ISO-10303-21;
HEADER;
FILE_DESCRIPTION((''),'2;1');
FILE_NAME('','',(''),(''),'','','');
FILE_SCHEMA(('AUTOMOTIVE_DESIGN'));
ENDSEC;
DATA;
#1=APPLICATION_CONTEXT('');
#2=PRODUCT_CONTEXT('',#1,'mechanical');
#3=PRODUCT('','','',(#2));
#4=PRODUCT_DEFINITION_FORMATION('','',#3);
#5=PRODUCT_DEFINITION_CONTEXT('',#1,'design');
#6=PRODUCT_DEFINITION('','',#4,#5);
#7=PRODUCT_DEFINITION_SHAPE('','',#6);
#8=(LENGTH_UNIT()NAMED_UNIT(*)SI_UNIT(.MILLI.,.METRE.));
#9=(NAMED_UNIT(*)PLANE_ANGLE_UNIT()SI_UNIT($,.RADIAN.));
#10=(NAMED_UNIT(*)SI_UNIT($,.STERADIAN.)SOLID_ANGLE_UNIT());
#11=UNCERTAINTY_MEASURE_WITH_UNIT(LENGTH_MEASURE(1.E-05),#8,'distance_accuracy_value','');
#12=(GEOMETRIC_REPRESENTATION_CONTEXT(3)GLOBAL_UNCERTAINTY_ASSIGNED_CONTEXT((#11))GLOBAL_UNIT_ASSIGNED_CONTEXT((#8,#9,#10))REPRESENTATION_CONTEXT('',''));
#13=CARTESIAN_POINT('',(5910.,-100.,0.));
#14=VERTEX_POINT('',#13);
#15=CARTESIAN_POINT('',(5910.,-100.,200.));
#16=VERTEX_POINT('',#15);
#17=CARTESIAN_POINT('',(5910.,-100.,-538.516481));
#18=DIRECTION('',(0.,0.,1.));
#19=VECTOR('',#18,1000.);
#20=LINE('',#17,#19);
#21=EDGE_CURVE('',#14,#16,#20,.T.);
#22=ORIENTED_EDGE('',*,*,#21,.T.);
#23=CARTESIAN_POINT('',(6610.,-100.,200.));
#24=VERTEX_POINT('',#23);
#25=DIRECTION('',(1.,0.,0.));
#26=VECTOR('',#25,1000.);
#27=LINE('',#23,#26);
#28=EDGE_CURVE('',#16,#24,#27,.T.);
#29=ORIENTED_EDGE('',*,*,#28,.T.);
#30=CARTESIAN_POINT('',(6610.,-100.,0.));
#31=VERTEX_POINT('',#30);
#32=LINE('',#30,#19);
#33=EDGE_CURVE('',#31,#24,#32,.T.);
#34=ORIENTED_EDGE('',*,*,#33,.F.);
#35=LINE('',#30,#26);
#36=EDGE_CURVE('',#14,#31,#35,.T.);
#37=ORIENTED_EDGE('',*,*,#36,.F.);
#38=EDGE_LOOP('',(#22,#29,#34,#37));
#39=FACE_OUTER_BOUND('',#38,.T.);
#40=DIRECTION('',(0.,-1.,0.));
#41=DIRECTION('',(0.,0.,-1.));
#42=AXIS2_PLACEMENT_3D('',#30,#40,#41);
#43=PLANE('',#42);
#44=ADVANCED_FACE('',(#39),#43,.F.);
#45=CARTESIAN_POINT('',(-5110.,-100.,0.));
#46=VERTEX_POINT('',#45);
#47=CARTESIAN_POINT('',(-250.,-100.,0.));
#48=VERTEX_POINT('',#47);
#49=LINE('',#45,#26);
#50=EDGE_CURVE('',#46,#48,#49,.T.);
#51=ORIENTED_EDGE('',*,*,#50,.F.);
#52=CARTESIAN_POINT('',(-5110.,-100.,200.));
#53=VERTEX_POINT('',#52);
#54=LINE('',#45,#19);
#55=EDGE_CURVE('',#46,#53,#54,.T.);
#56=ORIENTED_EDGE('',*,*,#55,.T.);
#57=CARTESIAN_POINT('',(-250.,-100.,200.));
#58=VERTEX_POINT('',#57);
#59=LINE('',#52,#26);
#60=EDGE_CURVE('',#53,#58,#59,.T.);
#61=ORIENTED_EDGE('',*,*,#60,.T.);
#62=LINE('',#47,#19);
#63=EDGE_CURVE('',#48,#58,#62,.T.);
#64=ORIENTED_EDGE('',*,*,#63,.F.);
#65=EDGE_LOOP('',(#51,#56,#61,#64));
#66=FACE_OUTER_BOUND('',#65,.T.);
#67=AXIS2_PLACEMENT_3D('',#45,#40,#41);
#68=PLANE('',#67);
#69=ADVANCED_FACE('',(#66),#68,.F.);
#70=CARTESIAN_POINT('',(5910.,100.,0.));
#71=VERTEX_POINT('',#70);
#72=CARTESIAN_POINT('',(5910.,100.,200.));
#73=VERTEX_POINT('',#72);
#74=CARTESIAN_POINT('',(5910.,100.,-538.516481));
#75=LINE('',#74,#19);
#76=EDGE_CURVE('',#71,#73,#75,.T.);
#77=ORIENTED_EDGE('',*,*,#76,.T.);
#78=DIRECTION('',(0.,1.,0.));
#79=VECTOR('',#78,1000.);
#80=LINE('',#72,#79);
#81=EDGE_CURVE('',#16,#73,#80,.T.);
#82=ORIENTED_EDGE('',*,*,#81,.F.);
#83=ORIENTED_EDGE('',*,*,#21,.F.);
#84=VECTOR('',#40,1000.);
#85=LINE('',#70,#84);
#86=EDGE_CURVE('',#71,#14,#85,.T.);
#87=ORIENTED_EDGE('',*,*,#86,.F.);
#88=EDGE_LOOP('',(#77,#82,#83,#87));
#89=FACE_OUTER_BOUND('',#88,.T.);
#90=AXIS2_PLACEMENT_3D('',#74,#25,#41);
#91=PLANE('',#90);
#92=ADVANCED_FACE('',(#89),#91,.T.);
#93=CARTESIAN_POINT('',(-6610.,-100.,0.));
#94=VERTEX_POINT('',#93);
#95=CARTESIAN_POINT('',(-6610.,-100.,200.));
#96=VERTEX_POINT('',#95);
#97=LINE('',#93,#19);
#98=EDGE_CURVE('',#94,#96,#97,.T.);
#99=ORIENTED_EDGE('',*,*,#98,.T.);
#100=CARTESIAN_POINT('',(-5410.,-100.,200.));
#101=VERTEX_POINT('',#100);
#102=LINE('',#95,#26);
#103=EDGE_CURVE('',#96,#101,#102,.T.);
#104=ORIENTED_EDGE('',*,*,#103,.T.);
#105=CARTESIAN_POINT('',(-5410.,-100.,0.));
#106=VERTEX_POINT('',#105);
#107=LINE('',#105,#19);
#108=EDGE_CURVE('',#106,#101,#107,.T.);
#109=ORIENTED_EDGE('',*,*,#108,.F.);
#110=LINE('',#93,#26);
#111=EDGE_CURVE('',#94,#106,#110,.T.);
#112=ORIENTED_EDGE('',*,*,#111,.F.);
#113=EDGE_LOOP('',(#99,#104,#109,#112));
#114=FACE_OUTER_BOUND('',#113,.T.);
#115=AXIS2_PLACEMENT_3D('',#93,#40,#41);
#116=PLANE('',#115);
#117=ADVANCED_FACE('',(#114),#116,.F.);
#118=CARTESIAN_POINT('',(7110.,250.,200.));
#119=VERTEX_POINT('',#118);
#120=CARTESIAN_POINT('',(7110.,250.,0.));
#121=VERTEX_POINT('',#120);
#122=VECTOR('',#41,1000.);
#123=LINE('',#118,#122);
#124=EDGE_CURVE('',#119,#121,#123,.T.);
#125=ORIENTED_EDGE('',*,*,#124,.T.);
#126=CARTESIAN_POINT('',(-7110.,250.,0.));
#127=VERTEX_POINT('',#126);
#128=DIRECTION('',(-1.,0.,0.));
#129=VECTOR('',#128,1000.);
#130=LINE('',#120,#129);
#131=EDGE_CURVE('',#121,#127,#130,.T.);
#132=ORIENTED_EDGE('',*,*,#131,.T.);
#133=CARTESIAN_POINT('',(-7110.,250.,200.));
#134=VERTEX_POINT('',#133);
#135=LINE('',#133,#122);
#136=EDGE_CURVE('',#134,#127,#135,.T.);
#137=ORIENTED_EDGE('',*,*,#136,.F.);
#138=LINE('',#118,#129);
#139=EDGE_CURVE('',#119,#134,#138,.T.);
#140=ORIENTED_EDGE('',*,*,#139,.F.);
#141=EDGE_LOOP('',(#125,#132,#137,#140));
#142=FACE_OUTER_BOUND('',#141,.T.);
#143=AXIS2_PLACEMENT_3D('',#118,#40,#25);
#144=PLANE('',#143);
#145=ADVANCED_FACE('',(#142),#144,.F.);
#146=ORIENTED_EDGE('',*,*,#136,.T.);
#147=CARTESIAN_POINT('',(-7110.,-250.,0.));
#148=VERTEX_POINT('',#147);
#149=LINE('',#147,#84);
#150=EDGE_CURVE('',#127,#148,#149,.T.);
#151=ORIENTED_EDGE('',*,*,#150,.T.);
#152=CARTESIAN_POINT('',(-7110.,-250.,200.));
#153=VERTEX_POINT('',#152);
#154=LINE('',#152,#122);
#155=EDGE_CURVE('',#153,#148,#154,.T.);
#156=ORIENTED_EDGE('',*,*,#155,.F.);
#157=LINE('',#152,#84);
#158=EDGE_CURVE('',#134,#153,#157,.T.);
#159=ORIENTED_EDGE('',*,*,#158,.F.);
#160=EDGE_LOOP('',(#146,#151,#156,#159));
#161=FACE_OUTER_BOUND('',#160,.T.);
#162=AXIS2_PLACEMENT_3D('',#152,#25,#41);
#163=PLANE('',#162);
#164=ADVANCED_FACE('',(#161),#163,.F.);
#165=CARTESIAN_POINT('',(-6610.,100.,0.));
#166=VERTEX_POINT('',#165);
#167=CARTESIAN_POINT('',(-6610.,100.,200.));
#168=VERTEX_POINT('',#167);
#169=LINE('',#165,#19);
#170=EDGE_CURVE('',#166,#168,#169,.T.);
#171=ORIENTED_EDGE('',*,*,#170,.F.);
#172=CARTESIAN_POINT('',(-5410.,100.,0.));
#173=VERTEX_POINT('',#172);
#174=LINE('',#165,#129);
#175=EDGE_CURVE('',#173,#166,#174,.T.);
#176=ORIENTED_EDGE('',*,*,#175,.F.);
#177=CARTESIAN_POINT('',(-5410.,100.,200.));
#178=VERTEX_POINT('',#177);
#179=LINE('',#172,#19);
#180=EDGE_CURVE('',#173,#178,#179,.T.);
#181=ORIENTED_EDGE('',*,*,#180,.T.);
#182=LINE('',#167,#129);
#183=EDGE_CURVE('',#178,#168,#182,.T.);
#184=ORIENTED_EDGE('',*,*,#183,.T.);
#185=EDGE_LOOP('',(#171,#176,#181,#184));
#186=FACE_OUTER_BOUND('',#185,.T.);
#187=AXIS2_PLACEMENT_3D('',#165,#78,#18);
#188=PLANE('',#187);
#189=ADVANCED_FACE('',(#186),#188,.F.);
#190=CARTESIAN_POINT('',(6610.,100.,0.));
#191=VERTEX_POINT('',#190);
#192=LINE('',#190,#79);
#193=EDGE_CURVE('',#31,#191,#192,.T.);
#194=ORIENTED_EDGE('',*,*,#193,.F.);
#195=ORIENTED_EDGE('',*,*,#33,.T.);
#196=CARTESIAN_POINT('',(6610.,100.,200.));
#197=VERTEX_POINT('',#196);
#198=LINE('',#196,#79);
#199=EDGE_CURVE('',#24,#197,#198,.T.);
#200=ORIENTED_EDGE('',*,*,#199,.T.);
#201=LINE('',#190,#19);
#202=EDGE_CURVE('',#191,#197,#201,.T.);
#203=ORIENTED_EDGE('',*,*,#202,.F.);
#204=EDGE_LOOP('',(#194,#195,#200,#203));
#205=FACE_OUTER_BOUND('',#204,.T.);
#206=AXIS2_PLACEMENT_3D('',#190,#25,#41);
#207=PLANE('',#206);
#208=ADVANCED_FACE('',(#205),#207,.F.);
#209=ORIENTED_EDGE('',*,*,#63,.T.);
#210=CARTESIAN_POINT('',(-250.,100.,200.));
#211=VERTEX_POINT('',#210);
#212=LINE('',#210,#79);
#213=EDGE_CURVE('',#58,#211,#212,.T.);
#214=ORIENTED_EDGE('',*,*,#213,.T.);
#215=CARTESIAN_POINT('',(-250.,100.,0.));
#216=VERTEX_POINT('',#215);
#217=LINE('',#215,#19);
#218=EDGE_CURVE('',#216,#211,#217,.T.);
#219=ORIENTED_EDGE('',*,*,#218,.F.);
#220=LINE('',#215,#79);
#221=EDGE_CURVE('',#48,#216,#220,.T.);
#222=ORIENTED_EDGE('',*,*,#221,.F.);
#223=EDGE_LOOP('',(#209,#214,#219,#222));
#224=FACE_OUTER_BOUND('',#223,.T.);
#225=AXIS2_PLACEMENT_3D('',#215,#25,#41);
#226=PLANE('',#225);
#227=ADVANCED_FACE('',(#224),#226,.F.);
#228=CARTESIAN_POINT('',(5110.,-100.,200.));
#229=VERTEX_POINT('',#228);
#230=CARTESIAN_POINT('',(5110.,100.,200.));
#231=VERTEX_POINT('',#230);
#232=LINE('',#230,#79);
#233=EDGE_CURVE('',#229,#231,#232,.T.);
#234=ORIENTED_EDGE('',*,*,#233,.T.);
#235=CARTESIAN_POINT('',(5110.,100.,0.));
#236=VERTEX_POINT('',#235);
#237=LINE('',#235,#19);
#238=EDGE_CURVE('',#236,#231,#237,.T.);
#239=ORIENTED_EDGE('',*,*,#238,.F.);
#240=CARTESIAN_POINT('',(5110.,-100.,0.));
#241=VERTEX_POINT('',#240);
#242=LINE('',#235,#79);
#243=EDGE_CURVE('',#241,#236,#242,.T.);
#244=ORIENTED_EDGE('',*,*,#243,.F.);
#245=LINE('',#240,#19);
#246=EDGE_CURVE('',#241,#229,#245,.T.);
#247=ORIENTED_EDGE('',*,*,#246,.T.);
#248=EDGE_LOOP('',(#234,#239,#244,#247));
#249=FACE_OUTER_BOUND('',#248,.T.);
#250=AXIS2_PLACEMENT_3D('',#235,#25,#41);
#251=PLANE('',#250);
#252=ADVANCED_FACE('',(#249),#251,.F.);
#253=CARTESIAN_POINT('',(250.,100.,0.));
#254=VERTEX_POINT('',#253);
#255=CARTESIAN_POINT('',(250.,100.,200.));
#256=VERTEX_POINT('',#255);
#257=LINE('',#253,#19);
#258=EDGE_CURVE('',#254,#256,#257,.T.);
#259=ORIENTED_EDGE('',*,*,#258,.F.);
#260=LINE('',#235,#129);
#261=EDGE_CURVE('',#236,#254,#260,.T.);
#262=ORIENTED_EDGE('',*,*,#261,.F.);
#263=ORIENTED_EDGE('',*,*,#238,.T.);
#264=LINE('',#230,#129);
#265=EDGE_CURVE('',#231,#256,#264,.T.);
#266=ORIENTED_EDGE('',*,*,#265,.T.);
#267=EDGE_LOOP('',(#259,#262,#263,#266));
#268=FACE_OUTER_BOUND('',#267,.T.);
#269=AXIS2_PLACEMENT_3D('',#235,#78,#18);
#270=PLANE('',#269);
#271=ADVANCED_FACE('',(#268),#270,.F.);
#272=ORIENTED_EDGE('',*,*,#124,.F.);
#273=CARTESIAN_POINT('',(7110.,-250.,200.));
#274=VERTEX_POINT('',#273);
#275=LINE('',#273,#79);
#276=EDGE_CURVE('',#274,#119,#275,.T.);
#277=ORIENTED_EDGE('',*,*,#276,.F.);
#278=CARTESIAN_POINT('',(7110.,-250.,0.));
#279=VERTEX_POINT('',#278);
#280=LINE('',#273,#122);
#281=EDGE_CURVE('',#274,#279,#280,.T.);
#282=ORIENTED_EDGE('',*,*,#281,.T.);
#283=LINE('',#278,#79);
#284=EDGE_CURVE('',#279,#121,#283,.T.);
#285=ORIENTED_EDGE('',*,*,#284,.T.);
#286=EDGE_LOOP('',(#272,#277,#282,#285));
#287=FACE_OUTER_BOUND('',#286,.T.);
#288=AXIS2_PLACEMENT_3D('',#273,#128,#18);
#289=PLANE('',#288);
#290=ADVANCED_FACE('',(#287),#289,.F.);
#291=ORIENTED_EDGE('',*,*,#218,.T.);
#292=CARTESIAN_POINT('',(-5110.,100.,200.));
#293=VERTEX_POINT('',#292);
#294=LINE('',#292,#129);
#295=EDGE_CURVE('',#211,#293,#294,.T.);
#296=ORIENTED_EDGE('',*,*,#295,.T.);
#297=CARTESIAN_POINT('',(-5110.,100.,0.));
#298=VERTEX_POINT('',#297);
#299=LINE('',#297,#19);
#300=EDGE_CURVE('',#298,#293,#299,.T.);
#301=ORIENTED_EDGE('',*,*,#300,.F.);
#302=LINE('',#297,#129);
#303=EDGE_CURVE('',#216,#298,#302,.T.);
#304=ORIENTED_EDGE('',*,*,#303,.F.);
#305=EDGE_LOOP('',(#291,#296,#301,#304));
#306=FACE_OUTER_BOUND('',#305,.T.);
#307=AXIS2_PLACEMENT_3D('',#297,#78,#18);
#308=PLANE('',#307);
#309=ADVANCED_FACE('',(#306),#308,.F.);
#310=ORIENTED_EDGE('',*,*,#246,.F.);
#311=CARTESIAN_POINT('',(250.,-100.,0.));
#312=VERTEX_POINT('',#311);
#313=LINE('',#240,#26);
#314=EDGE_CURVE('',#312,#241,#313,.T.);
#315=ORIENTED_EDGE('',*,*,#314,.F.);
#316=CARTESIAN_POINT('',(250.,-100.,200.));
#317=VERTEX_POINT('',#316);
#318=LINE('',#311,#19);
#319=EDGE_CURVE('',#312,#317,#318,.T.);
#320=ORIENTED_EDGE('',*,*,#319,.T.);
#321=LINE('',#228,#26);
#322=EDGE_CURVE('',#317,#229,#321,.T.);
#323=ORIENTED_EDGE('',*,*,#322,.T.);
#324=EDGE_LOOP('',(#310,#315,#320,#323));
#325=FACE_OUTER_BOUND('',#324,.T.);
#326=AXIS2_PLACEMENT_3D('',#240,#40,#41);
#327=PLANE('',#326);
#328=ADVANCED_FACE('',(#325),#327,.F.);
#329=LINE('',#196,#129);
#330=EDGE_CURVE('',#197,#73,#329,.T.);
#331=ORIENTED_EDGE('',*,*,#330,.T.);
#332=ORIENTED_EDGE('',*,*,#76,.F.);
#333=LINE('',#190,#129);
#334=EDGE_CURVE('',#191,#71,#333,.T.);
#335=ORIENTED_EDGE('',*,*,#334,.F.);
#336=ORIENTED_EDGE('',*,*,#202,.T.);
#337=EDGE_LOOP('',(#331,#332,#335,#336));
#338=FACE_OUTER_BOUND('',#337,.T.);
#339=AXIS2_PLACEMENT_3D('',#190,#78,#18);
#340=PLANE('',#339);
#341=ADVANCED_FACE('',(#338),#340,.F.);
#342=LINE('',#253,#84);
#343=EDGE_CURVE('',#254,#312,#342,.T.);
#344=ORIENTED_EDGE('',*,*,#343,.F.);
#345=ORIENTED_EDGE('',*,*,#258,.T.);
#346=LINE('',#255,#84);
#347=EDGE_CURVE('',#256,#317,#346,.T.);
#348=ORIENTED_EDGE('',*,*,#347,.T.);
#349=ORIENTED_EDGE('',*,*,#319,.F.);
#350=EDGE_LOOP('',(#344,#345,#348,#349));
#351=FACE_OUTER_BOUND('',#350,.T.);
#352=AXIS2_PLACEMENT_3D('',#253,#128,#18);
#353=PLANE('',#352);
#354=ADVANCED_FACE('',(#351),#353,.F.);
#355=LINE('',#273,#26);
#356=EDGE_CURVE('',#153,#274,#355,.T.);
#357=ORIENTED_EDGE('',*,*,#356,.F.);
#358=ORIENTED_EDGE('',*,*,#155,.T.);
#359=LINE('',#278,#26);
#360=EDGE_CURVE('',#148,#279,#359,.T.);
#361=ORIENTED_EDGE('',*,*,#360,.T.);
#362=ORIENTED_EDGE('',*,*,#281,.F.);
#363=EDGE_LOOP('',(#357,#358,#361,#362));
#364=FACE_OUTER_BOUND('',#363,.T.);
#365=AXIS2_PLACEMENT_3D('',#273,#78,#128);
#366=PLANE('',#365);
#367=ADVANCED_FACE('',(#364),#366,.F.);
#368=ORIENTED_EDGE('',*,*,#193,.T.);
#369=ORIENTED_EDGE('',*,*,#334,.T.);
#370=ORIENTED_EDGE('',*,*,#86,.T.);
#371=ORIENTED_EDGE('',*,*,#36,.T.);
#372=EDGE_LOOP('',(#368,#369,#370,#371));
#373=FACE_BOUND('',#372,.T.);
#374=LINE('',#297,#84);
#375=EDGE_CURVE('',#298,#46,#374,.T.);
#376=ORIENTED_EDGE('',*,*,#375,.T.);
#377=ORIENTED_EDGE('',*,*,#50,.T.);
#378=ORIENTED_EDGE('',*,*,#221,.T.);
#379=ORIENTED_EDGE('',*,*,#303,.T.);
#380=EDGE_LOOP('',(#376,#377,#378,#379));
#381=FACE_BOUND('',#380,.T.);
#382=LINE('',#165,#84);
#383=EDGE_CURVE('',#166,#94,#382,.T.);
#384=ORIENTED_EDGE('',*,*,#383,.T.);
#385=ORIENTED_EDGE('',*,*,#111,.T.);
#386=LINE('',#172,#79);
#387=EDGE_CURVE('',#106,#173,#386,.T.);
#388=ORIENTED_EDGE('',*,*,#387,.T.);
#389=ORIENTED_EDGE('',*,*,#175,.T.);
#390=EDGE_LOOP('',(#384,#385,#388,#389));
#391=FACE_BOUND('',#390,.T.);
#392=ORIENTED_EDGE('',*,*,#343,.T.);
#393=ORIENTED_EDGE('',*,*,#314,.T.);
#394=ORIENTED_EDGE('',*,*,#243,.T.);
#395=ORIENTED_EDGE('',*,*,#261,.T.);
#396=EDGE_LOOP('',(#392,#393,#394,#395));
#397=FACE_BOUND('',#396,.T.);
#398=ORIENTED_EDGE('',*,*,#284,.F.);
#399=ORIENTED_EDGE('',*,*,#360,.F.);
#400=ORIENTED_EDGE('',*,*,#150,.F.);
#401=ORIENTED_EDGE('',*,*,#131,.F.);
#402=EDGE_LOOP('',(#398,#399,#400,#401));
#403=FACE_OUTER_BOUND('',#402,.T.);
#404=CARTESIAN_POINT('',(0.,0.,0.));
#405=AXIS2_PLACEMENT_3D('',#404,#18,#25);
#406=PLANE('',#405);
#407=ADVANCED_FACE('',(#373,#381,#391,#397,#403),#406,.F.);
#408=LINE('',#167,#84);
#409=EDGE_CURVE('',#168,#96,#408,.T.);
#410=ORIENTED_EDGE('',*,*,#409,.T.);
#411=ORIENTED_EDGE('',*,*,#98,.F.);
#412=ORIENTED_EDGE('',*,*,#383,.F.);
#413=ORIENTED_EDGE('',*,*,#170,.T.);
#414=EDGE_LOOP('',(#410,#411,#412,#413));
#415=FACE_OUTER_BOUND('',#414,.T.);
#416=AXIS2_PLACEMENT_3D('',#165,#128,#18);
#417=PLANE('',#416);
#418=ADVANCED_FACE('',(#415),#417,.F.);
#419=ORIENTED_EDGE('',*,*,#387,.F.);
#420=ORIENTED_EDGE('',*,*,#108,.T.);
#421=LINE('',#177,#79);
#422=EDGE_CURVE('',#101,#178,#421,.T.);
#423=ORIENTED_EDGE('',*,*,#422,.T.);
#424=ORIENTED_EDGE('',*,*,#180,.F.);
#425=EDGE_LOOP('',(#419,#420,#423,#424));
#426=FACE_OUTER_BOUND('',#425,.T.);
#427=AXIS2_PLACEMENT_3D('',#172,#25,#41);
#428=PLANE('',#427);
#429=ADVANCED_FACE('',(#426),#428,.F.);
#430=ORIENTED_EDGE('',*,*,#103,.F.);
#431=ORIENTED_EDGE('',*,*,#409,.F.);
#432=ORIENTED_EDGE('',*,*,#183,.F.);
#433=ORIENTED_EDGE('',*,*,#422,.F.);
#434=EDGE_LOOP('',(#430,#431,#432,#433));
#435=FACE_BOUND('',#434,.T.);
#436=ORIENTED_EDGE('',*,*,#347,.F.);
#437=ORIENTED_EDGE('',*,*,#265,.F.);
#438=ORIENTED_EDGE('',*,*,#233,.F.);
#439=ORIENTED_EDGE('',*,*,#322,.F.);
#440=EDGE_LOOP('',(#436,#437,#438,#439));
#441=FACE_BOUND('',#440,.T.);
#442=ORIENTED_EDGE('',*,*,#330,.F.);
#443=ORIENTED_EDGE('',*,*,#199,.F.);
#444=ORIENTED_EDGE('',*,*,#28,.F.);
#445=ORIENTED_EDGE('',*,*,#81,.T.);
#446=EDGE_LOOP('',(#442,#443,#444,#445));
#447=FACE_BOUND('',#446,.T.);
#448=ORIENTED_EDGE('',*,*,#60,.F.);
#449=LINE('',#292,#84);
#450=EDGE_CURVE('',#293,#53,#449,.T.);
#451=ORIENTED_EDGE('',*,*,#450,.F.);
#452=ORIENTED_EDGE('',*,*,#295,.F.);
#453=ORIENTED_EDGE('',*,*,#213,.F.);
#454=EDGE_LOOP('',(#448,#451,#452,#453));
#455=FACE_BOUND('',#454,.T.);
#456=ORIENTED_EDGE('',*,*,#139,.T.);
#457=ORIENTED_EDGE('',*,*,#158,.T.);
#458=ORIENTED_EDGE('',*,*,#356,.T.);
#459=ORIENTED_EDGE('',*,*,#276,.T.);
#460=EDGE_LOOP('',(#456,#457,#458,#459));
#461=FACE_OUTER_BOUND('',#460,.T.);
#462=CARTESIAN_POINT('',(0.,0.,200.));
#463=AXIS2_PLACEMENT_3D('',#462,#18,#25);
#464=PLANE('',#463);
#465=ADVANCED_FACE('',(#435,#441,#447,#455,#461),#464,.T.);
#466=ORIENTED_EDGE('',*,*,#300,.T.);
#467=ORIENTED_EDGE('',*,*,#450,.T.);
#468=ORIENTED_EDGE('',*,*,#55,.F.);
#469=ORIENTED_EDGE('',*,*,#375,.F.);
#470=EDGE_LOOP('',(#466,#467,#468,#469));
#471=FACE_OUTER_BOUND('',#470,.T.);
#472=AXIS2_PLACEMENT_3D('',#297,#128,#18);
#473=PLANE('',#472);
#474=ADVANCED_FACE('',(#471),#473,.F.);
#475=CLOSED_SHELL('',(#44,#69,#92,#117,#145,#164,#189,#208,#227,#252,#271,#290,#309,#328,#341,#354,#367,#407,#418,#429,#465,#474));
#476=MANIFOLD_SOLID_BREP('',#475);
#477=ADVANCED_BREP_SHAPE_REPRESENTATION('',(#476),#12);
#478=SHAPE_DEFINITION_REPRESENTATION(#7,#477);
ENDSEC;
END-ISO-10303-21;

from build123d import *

# Parameters (mm, degrees)
SKETCH1_W           = 14220
SKETCH1_H           = 500
BOSS_EXTRUDE1_DEPTH = 200
SKETCH2_W           = 1200
SKETCH2_H           = 200
SKETCH2_W_2         = 4860
CUT_EXTRUDE1_DEPTH  = 7118.204507389
SKETCH4_W           = 500
SKETCH4_H           = 200
BOSS_EXTRUDE2_DEPTH = 200


with BuildPart() as part:
    # Sketch1 → Boss-Extrude1 (new body)
    with BuildSketch(Plane.XY):
        Rectangle(SKETCH1_W, SKETCH1_H)
    extrude(amount=BOSS_EXTRUDE1_DEPTH)

    # Sketch2 → Cut-Extrude1 (cut, through all)
    with BuildSketch(Plane.XY.offset(200)):
        with Locations((-6010, 0)):
            Rectangle(SKETCH2_W, SKETCH2_H)
        with Locations((-2680, 0)):
            Rectangle(SKETCH2_W_2, SKETCH2_H)
        with Locations((2680, 0)):
            Rectangle(SKETCH2_W_2, SKETCH2_H)
        with Locations((6010, 0)):
            Rectangle(SKETCH2_W, SKETCH2_H)
    extrude(amount=-CUT_EXTRUDE1_DEPTH, mode=Mode.SUBTRACT)

    # Sketch4 → Boss-Extrude2 (add)
    with BuildSketch(Plane.XY.offset(200)):
        with Locations((5660, 0)):
            Rectangle(SKETCH4_W, SKETCH4_H)
    extrude(amount=-BOSS_EXTRUDE2_DEPTH)


solid = part.part
